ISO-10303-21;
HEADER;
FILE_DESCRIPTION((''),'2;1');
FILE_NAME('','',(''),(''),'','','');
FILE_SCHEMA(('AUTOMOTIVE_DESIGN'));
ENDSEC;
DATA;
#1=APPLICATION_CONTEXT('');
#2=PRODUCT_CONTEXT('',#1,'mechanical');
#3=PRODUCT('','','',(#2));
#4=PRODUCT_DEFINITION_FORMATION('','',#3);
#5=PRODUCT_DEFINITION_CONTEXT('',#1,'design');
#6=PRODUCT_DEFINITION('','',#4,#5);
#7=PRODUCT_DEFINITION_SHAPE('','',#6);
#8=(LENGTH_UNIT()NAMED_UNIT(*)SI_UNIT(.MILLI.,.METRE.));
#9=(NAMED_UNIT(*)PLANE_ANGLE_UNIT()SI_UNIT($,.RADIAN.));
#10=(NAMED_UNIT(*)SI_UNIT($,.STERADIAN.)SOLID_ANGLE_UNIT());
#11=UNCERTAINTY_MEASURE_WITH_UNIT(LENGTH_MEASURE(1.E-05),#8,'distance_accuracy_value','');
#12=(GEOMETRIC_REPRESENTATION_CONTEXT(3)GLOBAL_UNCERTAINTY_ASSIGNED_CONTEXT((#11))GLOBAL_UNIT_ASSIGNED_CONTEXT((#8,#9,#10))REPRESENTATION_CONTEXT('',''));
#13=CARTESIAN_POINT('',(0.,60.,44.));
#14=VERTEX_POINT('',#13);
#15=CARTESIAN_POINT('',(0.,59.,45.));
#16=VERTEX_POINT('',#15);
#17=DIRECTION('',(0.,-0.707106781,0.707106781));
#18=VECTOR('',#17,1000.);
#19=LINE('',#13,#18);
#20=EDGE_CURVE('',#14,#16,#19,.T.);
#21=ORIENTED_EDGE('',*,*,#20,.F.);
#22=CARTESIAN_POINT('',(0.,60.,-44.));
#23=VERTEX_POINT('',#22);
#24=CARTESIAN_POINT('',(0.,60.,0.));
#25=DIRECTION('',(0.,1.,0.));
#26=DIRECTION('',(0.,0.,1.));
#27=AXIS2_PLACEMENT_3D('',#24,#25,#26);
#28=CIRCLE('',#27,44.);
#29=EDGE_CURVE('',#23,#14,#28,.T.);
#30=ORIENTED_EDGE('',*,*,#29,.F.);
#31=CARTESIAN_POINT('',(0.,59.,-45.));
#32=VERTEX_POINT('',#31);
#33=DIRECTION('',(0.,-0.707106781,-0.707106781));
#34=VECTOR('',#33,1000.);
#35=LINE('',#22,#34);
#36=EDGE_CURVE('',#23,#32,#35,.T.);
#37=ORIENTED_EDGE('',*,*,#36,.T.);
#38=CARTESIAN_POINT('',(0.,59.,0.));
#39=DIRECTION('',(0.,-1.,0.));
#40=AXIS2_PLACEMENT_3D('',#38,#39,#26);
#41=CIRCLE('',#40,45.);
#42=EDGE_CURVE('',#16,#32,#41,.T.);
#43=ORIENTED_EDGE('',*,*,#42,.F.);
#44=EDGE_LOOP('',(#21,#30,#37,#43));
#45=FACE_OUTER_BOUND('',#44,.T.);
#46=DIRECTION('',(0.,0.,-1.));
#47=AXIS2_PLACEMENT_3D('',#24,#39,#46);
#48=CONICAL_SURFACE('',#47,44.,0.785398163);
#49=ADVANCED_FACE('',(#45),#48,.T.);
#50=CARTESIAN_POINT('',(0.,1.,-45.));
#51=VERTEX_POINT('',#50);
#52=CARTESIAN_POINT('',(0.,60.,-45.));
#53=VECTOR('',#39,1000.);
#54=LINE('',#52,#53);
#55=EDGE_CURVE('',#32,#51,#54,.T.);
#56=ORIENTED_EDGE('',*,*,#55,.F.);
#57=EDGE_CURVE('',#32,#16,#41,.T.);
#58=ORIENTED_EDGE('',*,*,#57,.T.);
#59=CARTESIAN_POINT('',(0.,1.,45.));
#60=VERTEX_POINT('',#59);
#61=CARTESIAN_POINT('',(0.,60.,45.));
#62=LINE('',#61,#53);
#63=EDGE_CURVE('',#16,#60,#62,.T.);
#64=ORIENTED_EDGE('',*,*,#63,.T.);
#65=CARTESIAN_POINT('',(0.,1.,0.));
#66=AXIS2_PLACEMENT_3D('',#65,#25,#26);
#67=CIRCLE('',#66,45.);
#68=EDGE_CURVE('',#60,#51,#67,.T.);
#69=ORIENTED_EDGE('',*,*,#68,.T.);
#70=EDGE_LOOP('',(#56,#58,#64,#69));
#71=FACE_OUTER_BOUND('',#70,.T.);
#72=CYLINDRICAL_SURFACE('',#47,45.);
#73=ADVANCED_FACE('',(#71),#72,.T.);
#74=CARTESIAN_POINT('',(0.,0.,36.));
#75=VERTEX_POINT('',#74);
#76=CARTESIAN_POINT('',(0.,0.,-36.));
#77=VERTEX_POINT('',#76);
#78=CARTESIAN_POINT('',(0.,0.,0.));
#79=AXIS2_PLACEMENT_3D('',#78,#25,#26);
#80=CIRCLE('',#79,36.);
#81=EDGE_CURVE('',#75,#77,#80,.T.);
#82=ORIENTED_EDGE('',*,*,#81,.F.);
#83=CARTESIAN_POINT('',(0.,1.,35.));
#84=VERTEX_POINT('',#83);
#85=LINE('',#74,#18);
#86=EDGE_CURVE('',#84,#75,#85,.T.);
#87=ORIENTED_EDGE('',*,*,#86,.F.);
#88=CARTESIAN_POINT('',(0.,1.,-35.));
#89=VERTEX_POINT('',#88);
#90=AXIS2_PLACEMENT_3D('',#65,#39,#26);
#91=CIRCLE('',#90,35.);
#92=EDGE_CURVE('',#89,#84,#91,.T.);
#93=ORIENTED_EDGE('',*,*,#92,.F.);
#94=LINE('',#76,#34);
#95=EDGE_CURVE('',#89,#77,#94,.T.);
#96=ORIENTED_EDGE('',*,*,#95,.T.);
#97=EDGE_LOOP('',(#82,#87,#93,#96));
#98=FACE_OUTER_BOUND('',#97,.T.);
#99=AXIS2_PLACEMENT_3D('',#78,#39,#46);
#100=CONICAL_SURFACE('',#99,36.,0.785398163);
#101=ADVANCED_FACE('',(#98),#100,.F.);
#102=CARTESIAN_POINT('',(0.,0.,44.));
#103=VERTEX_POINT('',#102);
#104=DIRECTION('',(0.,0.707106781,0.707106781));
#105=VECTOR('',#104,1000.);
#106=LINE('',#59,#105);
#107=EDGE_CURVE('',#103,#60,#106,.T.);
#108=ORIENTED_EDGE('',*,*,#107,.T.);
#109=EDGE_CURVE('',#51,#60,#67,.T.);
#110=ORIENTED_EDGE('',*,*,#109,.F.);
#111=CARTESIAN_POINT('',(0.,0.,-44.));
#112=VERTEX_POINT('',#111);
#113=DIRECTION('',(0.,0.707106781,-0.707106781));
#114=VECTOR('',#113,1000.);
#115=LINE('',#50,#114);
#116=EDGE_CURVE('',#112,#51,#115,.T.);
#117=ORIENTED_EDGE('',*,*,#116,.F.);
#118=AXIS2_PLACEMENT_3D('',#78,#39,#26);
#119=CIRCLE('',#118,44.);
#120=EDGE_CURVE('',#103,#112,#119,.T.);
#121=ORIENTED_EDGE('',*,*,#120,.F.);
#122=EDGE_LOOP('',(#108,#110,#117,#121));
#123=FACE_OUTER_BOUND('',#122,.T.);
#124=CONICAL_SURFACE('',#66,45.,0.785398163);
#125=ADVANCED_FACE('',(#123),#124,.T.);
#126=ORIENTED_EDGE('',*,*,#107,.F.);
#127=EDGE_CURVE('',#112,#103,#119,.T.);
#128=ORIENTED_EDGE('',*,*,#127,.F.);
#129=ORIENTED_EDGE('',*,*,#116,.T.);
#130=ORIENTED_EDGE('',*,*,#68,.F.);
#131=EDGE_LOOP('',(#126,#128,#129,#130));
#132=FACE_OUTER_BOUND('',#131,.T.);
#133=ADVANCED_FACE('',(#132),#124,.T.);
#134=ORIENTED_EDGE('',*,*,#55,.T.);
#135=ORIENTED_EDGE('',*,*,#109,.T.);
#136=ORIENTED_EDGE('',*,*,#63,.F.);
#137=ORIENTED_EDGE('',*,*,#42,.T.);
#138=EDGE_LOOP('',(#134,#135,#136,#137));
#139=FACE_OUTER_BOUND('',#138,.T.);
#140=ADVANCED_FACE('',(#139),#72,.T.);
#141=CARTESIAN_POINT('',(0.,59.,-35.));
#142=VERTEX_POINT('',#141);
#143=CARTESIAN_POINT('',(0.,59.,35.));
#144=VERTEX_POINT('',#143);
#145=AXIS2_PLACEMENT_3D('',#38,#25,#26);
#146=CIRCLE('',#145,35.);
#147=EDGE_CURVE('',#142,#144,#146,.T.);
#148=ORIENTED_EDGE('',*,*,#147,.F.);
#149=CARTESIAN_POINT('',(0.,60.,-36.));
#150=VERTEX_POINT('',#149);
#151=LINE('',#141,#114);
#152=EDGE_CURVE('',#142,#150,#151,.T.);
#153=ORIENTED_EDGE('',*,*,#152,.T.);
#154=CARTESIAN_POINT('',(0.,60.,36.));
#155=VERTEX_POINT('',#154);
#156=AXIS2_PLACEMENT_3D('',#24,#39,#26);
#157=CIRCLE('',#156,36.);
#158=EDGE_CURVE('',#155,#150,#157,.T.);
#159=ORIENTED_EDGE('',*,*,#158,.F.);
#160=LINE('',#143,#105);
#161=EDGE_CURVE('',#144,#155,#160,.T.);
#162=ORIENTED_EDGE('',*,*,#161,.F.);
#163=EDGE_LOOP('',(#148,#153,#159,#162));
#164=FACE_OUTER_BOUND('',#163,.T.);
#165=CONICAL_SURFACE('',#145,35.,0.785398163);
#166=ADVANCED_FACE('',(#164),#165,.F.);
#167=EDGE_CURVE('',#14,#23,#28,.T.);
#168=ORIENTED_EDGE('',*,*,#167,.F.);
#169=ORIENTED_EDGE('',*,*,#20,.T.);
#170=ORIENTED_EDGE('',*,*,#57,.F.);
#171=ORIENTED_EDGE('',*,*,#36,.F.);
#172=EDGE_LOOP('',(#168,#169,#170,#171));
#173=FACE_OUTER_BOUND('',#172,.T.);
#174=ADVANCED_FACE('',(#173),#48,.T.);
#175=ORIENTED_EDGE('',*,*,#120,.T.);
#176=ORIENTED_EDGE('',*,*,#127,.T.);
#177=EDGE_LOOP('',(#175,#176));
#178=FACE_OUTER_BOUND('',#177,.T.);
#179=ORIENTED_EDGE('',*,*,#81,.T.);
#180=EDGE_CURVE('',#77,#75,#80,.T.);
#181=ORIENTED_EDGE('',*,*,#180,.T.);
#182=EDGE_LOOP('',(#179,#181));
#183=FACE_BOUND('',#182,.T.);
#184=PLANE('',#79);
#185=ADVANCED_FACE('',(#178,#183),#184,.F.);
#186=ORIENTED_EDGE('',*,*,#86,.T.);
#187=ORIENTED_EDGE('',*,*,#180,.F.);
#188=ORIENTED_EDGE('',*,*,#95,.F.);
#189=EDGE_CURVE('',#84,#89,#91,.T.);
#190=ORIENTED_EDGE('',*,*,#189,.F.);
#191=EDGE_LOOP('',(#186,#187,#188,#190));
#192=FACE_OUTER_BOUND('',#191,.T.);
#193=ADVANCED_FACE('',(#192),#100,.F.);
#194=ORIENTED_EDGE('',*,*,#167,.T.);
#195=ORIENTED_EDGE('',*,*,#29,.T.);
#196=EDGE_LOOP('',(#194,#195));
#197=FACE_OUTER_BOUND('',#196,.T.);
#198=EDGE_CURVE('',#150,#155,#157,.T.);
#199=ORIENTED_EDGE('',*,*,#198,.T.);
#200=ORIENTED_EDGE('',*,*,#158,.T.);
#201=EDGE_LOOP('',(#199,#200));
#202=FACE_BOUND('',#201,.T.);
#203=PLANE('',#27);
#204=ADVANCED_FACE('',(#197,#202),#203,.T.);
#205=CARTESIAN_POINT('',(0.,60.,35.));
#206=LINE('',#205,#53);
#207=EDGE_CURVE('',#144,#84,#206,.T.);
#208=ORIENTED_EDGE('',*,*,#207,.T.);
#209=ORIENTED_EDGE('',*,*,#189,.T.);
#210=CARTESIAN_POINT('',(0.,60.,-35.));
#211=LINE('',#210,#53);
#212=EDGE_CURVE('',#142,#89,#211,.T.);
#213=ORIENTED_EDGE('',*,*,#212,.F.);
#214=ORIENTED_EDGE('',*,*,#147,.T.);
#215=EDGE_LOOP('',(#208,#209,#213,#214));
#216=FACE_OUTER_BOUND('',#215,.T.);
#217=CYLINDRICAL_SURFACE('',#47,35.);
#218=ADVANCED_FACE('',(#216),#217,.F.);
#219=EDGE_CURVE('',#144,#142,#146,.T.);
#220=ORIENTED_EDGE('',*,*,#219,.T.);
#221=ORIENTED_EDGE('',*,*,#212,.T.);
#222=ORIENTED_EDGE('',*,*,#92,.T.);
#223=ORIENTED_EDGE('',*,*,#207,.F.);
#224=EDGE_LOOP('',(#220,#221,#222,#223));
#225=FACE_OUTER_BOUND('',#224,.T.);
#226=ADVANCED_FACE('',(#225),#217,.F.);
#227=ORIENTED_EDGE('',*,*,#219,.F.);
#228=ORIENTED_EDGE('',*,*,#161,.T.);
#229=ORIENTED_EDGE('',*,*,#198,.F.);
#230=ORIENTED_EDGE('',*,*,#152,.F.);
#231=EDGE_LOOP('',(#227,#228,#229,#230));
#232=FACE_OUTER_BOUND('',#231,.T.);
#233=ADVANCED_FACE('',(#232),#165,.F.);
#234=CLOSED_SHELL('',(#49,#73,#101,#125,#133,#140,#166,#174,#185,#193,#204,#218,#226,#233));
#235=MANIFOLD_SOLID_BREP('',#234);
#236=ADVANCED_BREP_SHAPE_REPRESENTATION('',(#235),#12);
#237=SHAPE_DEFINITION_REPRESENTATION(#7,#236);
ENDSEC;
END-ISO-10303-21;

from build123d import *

# Parameters (mm, degrees)
SKETCH1_R           = 45
SKETCH1_R_2         = 35
BOSS_EXTRUDE1_DEPTH = 60
CHAMFER2_SIZE       = 1


with BuildPart() as part:
    # Sketch1 → Boss-Extrude1 (new body)
    with BuildSketch(Plane(origin=(0, 0, 0), x_dir=(1, 0, 0), z_dir=(0, 1, 0))):
        with Locations(Location((0, 0, 0), (0, 0, 270))):
            Circle(SKETCH1_R)
        with Locations(Location((0, 0, 0), (0, 0, 270))):
            Circle(SKETCH1_R_2, mode=Mode.SUBTRACT)
    extrude(amount=BOSS_EXTRUDE1_DEPTH)

    # Chamfer2
    chamfer2_edges = [part.edges().sort_by_distance(p)[0] for p in [
        (0, 0, -45),
        (0, 60, -45),
        (0, 0, -35),
        (0, 60, -35),
    ]]
    chamfer(chamfer2_edges, length=CHAMFER2_SIZE)


solid = part.part
